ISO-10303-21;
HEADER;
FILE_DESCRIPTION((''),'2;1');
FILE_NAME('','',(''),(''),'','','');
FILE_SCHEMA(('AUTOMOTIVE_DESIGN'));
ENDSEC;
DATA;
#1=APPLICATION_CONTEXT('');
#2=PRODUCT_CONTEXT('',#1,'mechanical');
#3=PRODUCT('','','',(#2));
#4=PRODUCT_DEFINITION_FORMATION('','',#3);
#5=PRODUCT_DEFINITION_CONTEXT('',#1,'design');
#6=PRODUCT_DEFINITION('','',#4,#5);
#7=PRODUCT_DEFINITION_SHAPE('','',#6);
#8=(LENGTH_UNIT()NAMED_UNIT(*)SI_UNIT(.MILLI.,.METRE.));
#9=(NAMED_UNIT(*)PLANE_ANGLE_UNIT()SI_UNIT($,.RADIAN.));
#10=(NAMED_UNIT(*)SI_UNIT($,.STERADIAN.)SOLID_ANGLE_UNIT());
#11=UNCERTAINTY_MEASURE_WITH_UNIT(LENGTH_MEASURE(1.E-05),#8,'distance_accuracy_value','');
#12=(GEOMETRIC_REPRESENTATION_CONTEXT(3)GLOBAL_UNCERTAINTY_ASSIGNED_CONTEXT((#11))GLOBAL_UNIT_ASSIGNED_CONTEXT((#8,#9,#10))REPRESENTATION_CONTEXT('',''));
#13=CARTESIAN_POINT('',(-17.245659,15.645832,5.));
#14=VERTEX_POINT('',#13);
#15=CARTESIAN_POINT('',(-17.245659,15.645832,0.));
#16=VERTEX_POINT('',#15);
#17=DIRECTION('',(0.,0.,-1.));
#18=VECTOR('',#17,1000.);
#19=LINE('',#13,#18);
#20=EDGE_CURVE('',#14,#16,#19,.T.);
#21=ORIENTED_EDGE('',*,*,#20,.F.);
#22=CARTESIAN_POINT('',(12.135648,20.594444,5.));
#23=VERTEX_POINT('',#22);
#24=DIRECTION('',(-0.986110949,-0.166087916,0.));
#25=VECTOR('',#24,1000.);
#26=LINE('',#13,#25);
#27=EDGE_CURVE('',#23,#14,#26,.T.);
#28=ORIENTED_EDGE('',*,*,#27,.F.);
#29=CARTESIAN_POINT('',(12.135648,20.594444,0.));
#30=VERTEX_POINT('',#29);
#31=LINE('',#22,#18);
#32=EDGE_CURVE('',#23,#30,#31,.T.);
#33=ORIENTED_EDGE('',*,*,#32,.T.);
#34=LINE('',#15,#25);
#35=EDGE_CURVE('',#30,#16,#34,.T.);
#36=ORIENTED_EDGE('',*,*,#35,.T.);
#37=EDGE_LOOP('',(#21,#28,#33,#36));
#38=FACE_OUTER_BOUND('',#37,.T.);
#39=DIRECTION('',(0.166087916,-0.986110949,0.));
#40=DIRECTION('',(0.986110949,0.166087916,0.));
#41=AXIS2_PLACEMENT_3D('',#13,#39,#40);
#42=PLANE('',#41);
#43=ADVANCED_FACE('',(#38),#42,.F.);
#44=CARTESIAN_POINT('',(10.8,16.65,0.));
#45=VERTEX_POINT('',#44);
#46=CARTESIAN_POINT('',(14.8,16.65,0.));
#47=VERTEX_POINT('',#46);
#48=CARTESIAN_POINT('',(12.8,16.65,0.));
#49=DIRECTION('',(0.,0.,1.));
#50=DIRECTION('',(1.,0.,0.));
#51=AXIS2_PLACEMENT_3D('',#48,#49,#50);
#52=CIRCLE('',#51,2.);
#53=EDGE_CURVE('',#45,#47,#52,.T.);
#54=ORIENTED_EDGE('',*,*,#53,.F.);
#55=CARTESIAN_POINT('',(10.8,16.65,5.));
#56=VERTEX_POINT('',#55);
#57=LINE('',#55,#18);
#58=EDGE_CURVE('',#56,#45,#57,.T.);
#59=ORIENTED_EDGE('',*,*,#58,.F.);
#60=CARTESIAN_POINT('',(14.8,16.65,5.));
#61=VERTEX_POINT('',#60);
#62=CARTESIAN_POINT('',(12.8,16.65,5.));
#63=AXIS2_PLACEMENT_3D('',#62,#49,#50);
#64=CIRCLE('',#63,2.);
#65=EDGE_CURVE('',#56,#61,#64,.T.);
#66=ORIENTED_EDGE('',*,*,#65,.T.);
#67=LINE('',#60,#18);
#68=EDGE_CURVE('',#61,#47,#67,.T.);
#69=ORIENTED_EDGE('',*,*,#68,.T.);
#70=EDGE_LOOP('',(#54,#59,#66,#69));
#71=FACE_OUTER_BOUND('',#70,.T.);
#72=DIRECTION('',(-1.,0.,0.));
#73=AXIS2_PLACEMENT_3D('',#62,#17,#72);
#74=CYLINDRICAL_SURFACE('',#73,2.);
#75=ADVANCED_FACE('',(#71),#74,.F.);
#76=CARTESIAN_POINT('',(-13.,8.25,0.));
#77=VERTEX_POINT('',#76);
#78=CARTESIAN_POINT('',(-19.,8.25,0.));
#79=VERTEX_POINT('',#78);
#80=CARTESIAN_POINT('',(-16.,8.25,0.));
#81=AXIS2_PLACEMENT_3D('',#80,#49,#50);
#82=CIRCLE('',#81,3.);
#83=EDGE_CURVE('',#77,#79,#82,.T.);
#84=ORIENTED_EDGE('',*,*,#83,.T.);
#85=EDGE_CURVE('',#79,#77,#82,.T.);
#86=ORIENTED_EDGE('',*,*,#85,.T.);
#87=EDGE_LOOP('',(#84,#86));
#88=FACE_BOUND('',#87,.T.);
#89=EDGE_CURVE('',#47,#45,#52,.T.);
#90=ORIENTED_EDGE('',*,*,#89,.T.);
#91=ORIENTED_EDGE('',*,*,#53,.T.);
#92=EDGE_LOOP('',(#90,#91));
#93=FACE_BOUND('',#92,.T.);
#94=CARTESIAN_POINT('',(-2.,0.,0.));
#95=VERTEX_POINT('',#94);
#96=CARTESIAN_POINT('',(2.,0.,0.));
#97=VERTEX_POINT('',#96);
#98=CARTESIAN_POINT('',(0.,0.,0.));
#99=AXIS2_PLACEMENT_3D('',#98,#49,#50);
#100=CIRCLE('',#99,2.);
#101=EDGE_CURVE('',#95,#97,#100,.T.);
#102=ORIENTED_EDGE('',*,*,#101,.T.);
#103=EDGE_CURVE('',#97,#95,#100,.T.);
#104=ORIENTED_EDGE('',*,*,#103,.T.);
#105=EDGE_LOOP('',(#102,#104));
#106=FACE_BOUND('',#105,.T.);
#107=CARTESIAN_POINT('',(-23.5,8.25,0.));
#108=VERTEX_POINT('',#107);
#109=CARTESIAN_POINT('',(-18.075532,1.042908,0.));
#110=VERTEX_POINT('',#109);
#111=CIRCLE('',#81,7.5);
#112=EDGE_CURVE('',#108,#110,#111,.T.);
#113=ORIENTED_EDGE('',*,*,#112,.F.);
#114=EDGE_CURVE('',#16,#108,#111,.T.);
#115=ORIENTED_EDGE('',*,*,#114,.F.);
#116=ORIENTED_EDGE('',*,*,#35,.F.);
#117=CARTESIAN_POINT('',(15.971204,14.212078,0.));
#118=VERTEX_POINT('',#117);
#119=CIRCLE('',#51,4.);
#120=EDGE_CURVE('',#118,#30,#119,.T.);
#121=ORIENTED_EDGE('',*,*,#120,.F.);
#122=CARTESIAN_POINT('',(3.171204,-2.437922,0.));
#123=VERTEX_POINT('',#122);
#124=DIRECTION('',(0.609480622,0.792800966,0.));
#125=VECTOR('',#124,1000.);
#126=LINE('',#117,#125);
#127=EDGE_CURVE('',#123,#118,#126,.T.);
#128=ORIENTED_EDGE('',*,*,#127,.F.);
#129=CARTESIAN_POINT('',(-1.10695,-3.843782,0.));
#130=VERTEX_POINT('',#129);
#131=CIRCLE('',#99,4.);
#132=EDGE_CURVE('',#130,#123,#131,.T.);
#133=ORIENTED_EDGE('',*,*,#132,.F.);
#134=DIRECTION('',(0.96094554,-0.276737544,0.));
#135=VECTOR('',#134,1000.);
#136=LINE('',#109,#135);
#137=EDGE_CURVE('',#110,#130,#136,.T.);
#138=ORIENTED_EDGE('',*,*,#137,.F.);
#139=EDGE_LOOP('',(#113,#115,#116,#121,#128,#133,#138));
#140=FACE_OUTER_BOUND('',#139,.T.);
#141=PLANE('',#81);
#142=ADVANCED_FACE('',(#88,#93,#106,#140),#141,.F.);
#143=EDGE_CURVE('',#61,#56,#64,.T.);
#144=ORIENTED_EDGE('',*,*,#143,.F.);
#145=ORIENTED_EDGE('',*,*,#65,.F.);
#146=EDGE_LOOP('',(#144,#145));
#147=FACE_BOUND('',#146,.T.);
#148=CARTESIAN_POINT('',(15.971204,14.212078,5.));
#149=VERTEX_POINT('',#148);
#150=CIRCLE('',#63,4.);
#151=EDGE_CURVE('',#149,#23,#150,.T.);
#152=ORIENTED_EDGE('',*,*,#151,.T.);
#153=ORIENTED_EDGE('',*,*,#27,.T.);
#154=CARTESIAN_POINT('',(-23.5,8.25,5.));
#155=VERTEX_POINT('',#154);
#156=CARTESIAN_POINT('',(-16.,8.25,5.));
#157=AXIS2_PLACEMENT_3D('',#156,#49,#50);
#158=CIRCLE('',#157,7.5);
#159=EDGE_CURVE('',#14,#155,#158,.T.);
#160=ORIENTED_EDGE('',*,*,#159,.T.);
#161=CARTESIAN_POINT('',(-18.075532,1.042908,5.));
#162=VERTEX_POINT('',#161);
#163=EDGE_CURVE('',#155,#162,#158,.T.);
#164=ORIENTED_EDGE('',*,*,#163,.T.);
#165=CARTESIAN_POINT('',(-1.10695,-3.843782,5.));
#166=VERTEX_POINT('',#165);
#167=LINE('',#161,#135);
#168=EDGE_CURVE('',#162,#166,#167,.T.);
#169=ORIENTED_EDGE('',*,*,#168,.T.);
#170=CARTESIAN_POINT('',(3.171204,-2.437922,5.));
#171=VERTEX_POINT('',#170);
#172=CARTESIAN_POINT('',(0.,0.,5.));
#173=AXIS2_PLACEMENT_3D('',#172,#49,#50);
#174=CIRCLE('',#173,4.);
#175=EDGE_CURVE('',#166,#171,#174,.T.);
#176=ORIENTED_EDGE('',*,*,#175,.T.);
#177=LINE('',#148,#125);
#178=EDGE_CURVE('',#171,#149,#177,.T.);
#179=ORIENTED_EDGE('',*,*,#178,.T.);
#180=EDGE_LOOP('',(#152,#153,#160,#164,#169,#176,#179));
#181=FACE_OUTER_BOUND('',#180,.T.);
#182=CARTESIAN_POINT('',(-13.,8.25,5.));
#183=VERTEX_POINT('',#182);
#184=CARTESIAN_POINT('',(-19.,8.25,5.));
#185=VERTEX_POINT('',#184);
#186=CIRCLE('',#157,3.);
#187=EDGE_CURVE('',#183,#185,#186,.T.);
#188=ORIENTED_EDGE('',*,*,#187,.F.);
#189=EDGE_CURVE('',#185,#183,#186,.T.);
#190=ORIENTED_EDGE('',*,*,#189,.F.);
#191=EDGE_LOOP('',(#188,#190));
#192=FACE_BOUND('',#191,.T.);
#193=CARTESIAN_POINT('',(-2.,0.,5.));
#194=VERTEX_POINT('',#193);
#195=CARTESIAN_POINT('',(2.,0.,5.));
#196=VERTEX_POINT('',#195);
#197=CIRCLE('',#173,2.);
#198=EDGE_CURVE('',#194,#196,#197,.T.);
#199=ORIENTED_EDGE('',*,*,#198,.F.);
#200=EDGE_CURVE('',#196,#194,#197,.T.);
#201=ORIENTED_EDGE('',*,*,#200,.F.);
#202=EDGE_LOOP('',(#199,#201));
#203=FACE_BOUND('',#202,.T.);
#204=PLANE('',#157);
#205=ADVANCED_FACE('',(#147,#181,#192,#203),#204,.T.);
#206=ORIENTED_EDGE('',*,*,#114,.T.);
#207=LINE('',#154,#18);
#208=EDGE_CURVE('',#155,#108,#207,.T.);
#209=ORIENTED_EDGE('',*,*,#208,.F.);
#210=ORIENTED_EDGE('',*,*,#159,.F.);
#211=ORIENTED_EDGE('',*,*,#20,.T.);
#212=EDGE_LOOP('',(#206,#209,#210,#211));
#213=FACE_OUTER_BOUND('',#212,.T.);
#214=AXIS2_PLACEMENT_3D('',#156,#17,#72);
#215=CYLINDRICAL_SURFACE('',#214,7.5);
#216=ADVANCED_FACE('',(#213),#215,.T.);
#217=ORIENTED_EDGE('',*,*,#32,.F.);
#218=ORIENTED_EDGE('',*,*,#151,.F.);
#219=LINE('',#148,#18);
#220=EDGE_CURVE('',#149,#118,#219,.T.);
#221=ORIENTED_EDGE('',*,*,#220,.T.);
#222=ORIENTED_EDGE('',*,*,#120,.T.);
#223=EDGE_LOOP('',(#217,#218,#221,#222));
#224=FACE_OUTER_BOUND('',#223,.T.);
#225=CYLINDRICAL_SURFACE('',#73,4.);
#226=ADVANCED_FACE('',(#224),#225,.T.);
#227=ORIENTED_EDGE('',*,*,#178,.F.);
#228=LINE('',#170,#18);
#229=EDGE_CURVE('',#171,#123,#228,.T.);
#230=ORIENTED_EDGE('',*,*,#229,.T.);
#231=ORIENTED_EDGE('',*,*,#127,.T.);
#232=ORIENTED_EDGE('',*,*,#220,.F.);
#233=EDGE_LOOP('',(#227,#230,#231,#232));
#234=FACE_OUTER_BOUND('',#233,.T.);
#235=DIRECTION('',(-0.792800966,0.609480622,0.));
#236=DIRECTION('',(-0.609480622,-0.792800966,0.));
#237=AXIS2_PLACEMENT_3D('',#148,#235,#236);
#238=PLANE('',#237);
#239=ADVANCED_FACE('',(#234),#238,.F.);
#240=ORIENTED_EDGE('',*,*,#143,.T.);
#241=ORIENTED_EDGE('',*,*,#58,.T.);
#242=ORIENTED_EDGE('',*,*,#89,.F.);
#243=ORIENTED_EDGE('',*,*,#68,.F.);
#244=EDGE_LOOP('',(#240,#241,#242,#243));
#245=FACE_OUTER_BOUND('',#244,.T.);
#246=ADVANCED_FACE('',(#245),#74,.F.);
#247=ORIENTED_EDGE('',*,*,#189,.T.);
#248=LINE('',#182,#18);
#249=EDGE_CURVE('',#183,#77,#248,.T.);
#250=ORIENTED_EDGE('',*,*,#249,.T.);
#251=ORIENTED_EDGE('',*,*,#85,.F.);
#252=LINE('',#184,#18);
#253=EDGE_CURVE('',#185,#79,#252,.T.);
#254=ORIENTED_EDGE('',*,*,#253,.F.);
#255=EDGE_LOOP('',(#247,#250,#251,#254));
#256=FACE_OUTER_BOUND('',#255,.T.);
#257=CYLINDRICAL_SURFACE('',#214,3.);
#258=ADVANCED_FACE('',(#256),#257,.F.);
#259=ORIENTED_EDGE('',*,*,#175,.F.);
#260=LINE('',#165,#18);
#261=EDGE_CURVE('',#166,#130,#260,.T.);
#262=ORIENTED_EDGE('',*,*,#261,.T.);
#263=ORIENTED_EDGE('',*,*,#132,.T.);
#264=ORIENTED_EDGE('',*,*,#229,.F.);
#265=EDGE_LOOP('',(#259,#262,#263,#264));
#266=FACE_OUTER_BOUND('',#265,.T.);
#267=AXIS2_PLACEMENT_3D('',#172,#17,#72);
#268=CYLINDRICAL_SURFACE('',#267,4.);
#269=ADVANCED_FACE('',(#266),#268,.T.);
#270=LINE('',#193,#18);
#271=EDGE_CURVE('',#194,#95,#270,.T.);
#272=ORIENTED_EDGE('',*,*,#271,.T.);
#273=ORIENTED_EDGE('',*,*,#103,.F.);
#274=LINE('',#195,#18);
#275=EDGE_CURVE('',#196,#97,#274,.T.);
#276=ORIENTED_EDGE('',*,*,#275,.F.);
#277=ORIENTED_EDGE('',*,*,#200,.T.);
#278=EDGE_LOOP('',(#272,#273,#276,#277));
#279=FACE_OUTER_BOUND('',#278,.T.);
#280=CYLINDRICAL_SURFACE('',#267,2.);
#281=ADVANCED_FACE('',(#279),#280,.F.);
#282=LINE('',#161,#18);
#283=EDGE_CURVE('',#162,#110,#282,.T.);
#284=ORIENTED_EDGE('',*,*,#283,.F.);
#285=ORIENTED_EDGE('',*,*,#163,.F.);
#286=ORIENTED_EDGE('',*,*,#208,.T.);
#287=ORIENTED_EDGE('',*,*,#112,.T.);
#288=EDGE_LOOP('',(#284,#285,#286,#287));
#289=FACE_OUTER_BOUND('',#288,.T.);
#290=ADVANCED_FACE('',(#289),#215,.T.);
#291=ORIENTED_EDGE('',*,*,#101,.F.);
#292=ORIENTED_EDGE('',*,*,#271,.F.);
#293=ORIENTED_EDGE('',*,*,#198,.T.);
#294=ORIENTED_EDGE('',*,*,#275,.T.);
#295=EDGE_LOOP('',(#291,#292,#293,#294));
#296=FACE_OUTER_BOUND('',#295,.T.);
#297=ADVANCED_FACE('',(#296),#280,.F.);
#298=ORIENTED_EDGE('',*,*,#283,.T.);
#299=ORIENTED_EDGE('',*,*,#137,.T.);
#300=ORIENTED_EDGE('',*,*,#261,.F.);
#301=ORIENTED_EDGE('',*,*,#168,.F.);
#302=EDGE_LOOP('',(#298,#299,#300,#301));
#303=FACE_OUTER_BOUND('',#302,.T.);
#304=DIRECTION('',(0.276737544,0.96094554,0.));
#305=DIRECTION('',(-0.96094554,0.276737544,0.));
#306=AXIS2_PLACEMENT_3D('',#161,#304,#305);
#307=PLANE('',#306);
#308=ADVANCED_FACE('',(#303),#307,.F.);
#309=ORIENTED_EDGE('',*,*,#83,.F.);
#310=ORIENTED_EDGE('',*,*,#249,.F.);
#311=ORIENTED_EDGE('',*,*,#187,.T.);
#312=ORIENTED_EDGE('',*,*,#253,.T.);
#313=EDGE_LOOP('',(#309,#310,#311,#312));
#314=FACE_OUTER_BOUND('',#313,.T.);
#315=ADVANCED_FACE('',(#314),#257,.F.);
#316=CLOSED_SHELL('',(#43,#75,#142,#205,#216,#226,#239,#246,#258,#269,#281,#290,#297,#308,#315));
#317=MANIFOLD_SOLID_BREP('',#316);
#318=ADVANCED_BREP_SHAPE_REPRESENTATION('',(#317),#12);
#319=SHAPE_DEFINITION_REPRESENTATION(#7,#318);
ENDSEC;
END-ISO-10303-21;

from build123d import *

# Parameters (mm, degrees)
SKETCH1_R           = 2
SKETCH1_R_2         = 3
BOSS_EXTRUDE1_DEPTH = 5


with BuildPart() as part:
    # Sketch1 → Boss-Extrude1 (new body)
    with BuildSketch(Plane.XY):
        with BuildLine():
            Line((-17.245659368, 15.645832119), (12.135648337, 20.594443797))
            ThreePointArc((12.135648337, 20.594443797), (16.228516711, 18.710406067), (15.971203863, 14.212077511))
            Line((15.971203863, 14.212077511), (3.171203863, -2.437922489))
            ThreePointArc((3.171203863, -2.437922489), (1.248757853, -3.80007945), (-1.106950177, -3.843782162))
            Line((-1.106950177, -3.843782162), (-18.075531582, 1.042908447))
            ThreePointArc((-18.075531582, 1.042908447), (-23.487918421, 8.675532282), (-17.245659368, 15.645832119))
        make_face()
        Circle(SKETCH1_R, mode=Mode.SUBTRACT)
        with Locations((-16, 8.25)):
            Circle(SKETCH1_R_2, mode=Mode.SUBTRACT)
        with Locations((12.8, 16.65)):
            Circle(SKETCH1_R, mode=Mode.SUBTRACT)
    extrude(amount=BOSS_EXTRUDE1_DEPTH)


solid = part.part
